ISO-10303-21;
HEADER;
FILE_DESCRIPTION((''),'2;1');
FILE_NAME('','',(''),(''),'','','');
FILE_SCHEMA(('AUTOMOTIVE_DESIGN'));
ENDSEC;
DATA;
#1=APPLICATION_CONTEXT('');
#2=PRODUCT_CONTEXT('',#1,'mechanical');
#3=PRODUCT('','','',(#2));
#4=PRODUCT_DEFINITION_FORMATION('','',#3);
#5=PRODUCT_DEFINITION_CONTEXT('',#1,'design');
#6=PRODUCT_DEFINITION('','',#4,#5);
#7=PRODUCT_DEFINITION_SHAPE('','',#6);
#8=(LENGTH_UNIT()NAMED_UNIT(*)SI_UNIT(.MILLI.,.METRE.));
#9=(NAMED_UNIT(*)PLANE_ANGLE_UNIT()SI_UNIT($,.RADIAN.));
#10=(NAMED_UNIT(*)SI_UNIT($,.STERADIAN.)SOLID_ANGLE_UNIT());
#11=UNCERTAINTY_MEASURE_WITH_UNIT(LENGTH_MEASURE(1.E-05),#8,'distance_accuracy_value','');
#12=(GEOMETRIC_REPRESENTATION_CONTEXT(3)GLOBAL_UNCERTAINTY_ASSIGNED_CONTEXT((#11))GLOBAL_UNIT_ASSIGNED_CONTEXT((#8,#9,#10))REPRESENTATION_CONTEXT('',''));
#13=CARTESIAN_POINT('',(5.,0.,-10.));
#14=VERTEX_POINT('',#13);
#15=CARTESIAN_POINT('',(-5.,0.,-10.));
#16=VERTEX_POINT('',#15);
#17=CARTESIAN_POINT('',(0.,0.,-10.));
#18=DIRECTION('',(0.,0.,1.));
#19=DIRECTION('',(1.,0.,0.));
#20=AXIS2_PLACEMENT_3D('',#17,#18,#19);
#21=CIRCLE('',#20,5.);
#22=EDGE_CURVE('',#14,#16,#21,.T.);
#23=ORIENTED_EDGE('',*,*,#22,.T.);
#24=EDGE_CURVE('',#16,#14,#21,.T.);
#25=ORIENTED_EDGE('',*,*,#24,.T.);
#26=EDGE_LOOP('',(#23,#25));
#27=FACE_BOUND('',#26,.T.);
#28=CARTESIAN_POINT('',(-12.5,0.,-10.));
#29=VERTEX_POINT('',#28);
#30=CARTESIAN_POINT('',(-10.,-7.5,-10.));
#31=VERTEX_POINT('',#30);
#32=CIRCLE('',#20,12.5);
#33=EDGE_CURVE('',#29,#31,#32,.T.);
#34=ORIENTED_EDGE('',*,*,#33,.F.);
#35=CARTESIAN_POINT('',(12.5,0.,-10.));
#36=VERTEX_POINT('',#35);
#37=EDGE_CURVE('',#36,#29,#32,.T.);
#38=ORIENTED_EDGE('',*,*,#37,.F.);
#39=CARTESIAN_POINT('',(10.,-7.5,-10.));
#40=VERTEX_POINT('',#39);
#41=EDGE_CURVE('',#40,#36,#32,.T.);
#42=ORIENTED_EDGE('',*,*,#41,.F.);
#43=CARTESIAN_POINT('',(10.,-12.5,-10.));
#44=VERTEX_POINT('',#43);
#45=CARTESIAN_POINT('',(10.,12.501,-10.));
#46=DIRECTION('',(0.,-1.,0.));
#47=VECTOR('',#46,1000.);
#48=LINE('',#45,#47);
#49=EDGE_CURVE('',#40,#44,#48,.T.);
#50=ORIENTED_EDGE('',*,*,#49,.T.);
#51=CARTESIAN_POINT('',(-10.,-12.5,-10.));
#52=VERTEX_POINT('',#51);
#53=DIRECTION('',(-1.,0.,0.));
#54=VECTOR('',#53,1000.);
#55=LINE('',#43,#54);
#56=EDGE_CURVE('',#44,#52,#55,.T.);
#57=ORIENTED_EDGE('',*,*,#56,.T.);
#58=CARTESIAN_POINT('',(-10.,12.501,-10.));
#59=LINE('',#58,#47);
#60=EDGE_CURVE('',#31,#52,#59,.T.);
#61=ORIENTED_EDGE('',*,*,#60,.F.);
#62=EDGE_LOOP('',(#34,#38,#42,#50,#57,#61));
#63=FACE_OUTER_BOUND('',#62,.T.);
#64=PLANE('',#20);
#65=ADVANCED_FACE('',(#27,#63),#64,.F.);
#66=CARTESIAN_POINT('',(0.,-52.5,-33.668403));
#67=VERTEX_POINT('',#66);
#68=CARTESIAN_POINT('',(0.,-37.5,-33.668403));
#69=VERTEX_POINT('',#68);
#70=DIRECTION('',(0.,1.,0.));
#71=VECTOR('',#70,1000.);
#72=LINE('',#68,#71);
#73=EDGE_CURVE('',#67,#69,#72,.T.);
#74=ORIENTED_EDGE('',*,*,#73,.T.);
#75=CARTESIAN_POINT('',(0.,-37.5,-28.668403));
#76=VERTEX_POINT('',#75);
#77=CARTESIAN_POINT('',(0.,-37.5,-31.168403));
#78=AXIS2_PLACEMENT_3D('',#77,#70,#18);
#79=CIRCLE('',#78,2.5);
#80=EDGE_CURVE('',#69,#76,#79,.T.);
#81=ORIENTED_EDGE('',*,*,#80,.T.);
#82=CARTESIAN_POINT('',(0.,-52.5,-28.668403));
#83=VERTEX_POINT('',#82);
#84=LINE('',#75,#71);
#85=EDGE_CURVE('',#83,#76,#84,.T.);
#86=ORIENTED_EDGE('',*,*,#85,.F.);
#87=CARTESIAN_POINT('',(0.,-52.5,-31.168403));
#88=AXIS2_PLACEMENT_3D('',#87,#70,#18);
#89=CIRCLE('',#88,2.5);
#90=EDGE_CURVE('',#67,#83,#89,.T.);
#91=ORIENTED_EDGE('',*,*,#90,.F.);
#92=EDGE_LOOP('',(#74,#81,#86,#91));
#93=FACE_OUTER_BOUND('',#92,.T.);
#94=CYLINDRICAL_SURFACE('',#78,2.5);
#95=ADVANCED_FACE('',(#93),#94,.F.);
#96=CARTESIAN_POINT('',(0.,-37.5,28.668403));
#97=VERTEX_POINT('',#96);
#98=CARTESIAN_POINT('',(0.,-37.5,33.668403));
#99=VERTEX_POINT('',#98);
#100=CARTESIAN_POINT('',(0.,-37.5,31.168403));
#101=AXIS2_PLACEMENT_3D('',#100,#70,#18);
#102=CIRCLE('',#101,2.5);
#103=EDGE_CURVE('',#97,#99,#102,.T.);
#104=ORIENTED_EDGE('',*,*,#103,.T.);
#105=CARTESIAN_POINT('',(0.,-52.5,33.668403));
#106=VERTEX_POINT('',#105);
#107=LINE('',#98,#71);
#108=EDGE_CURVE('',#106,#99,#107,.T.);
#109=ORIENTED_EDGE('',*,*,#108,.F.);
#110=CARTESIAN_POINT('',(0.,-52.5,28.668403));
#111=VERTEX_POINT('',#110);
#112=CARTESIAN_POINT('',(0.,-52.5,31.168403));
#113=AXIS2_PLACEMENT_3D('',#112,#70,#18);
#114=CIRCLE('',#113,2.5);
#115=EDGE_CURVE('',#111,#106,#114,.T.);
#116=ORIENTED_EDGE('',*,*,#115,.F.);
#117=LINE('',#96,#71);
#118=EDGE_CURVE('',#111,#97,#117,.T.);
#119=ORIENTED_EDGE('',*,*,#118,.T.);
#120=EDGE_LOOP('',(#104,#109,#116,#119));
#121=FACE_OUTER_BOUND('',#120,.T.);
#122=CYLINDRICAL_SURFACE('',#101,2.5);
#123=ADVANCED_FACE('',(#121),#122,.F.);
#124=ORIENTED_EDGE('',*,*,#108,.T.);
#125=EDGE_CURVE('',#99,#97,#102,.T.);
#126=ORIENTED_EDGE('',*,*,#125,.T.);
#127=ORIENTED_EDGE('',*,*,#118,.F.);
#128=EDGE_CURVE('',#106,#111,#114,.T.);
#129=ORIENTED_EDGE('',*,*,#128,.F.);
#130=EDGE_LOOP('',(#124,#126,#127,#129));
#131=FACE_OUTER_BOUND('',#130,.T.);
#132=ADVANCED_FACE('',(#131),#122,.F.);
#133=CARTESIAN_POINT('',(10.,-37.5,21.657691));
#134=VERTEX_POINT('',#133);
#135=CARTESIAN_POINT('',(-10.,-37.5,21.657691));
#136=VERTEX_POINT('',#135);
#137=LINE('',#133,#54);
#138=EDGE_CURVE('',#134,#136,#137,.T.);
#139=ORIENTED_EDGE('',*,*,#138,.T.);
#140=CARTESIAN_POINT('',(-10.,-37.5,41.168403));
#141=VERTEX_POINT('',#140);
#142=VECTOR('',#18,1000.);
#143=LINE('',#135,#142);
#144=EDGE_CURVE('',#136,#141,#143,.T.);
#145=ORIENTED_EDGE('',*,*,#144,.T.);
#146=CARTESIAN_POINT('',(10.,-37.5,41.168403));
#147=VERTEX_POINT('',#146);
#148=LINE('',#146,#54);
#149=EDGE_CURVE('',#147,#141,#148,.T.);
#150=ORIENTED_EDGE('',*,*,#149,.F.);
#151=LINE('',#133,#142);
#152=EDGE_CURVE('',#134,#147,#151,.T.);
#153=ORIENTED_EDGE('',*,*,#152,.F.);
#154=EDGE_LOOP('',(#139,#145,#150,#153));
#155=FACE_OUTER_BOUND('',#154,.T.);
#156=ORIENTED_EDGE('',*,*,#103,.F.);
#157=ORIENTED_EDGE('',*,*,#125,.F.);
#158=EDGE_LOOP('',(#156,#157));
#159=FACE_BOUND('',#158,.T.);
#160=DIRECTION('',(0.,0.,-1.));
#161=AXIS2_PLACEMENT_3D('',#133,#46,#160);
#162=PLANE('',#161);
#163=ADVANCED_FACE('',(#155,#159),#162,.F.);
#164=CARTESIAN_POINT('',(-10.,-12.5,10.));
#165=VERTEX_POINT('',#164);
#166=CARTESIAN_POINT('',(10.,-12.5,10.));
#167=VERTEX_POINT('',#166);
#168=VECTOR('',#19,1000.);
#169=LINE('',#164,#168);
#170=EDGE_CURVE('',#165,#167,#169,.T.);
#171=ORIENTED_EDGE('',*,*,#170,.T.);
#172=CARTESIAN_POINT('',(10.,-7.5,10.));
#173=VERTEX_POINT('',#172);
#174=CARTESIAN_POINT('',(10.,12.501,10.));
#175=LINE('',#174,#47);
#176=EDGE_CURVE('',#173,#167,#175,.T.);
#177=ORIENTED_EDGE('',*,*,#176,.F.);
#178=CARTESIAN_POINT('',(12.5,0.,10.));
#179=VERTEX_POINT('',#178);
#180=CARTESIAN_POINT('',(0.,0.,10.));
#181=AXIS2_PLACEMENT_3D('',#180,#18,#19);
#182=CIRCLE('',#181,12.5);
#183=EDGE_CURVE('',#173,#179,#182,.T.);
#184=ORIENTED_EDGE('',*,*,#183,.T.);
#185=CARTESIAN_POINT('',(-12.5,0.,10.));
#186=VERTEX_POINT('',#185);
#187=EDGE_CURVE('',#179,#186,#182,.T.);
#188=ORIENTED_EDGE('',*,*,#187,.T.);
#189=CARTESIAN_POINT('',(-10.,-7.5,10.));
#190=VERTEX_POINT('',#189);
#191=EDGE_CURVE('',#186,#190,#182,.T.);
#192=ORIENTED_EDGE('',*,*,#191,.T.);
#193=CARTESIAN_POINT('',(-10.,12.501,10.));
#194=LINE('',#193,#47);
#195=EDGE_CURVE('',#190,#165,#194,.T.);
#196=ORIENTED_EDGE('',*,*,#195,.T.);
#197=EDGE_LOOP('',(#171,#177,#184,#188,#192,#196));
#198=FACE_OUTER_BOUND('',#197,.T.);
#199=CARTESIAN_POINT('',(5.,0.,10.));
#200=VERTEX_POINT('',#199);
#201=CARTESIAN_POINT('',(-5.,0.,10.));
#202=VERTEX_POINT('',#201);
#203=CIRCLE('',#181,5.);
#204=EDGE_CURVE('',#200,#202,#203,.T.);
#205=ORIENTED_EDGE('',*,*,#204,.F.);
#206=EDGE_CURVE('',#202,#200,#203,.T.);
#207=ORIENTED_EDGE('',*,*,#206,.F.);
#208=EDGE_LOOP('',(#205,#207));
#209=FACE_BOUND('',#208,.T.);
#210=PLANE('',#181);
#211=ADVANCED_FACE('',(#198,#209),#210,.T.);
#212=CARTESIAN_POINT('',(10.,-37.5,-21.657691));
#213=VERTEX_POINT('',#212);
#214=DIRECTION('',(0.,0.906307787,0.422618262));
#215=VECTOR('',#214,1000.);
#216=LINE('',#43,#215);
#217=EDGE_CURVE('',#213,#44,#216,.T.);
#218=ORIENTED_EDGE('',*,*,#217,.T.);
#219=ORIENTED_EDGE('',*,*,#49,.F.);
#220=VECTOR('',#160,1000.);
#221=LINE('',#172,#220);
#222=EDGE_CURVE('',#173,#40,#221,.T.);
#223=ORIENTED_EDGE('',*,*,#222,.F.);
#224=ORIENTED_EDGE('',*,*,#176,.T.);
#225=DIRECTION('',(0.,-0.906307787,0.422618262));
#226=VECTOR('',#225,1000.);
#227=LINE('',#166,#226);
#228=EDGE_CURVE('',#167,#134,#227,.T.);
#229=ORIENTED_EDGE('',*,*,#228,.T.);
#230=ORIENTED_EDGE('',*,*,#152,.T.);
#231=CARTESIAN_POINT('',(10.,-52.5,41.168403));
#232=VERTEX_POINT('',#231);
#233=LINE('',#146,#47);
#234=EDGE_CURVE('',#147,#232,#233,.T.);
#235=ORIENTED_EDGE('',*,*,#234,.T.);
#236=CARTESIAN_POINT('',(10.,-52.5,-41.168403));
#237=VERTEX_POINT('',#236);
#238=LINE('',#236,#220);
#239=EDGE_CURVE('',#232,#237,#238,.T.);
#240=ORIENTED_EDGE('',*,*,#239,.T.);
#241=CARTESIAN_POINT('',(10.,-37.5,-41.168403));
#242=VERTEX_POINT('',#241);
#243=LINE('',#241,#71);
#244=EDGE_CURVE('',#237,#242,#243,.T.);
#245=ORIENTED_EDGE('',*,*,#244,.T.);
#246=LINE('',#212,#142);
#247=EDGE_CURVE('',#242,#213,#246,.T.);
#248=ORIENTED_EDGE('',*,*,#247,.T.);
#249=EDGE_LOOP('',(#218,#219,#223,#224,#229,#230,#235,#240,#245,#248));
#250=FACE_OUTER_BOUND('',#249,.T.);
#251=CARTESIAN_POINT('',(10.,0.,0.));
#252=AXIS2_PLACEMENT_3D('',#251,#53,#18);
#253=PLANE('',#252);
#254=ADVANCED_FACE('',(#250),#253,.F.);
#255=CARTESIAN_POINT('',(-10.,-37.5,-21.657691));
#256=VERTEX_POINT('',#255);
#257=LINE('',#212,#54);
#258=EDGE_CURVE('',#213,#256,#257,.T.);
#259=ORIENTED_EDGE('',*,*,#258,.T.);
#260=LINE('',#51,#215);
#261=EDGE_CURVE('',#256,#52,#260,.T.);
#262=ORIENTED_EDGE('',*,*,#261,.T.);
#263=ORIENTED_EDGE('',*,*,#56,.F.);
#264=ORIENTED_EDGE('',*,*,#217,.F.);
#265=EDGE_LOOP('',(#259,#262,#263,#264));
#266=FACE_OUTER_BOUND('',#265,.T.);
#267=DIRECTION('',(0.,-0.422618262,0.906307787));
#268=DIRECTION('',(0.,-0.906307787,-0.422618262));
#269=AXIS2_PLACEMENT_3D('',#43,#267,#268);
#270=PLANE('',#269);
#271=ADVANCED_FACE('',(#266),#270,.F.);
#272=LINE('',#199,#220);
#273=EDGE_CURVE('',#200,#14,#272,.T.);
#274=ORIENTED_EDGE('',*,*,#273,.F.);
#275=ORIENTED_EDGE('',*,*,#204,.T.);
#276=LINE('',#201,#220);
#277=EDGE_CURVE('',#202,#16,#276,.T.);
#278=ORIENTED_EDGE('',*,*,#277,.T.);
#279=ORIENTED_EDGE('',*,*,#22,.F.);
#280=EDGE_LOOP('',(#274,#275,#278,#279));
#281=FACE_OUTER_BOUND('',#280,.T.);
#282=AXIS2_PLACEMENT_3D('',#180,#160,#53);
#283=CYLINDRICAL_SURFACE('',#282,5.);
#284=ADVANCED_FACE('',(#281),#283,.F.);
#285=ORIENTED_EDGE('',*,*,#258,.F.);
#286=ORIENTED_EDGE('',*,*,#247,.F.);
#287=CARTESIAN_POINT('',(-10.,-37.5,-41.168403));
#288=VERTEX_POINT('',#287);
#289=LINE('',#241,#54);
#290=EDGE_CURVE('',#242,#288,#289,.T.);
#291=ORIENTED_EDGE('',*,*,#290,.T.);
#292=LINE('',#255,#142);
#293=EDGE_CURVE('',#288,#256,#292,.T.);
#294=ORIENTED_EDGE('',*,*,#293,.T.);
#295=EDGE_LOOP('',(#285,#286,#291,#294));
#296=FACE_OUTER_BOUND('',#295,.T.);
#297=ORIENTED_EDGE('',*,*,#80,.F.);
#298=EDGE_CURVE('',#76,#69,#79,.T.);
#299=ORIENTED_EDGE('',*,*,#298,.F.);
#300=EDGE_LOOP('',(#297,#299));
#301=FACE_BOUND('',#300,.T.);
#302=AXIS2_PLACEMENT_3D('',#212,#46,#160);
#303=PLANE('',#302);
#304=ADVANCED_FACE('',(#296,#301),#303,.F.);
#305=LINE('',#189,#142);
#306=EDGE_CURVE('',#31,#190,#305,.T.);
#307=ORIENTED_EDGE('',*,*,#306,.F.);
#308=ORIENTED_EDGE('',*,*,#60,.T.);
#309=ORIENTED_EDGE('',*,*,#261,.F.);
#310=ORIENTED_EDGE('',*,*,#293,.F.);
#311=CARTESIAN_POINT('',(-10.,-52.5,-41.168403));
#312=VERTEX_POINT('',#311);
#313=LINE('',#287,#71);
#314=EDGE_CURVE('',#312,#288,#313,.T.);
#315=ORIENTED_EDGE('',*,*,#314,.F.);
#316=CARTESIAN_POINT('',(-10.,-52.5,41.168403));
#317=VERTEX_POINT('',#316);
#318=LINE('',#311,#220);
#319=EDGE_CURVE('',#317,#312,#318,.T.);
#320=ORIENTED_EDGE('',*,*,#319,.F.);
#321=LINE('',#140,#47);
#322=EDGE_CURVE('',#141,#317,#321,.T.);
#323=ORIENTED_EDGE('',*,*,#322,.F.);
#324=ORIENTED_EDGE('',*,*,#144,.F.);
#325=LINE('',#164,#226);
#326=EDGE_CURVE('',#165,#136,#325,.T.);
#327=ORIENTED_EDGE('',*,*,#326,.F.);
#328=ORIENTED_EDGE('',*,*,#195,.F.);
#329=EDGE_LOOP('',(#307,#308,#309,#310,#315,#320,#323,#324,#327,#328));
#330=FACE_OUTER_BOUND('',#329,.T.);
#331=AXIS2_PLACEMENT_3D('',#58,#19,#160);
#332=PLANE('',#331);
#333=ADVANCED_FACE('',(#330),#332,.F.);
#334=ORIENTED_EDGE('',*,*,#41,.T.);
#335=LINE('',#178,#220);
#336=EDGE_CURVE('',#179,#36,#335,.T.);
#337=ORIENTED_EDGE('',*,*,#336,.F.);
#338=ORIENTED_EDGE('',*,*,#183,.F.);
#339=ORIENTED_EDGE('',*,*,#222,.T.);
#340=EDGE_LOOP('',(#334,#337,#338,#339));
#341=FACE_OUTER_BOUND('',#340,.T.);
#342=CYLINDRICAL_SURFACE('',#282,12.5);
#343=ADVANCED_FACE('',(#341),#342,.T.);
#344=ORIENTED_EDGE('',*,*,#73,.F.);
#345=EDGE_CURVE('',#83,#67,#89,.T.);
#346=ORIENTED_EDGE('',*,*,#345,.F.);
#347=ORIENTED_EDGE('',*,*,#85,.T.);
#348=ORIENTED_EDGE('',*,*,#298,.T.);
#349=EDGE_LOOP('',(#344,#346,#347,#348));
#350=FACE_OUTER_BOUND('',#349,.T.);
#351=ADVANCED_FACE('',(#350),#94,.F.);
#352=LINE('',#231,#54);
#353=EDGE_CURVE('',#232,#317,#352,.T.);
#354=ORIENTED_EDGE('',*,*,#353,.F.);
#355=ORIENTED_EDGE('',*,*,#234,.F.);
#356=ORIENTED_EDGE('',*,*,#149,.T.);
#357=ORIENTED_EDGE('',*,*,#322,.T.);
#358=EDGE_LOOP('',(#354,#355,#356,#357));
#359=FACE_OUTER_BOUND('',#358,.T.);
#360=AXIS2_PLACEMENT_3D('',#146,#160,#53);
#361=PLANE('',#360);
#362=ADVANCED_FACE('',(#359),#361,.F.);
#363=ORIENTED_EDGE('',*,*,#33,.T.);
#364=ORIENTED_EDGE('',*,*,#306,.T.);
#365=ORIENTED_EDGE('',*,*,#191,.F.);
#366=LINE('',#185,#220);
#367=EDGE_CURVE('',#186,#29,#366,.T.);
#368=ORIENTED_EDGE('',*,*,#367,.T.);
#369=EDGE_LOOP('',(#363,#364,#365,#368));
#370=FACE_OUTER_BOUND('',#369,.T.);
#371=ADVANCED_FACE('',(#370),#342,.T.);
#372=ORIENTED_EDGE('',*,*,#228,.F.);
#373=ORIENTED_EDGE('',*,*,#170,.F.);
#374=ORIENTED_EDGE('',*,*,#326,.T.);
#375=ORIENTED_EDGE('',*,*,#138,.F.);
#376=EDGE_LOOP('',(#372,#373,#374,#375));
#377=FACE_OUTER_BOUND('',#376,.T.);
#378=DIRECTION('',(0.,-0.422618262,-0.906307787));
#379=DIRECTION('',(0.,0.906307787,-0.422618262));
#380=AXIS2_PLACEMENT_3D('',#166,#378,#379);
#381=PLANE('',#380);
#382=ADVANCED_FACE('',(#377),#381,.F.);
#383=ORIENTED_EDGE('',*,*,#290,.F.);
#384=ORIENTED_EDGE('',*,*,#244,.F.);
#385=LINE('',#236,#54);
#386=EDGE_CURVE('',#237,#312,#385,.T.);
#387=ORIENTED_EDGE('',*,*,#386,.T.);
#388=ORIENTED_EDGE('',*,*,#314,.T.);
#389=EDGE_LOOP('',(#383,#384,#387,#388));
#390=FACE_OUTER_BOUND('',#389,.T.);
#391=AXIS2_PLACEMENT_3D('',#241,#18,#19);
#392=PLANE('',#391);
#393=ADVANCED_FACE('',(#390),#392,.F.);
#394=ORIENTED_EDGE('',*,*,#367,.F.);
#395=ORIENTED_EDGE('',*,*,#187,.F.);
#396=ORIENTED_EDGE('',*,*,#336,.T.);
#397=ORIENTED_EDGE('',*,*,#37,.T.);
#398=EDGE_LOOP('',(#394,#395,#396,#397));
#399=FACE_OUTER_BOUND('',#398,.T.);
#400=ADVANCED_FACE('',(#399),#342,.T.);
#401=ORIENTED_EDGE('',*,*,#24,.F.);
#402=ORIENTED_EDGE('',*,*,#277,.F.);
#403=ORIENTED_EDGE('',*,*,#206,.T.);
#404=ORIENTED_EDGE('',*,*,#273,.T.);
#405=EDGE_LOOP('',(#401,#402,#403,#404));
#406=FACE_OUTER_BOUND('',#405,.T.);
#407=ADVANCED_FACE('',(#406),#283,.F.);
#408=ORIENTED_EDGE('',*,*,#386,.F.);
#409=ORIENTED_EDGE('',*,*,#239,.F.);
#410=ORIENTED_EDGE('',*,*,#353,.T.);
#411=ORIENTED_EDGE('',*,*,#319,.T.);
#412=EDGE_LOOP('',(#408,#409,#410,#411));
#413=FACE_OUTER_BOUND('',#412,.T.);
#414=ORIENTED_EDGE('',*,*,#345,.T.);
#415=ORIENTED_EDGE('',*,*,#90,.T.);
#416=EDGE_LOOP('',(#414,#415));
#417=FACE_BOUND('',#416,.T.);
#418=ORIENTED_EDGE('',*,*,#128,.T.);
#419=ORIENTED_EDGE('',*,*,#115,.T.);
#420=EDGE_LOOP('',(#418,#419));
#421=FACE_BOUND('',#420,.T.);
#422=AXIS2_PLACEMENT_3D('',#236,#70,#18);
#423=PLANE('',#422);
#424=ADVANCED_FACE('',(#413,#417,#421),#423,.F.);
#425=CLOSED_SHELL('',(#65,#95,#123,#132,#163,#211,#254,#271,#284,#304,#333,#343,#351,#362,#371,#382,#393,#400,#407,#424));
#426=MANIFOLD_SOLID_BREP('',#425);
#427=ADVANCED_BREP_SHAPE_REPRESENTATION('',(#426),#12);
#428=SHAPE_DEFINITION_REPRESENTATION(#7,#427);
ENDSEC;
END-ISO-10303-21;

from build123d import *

# Parameters (mm, degrees)
SKETCH_1_R           = 12.5
SKETCH_1_R_2         = 5
EXTRUDE_1_DEPTH      = 10
EXTRUDE_3_DEPTH      = 10
EXTRUDE_4_REACH      = 60.746
EXTRUDE_4_END_RADIUS = 12.5
SKETCH_6_W           = 20
SKETCH_6_H           = 20
HOLE_WIZARD_M6_1_D   = 5


with BuildPart() as part:
    # 草图1 → 凸台-拉伸1 (new, symmetric)
    with BuildSketch(Plane.XY):
        Circle(SKETCH_1_R)
        Circle(SKETCH_1_R_2, mode=Mode.SUBTRACT)
    extrude(amount=EXTRUDE_1_DEPTH, both=True)



with BuildPart() as body_2:
    # 草图5 → 凸台-拉伸3 (new, symmetric)
    with BuildSketch(Plane(origin=(0, 0, 0), x_dir=(0, 0, -1), z_dir=(1, 0, 0))):
        Polygon((10, -12.5), (21.657691454, -37.5), (41.168402769, -37.5), (41.168402769, -52.5), (-41.168402769, -52.5), (-41.168402769, -37.5), (-21.657691454, -37.5), (-10, -12.5), align=None)
    extrude(amount=EXTRUDE_3_DEPTH, both=True)


with BuildPart() as part_1:
    add(part.part)

    add(body_2.part)  # 凸台-拉伸4 merges body 2
    # 凸台-拉伸4: up to this cylinder (the profile starts outside it)
    extrude_4_end = Plane(origin=(0, 0, 0), z_dir=(0, 0, -1)) * Cylinder(EXTRUDE_4_END_RADIUS, 147.492, mode=Mode.PRIVATE)
    # 草图6 → 凸台-拉伸4 (add, up to the surface)
    with BuildSketch(Plane(origin=(0, -12.5, 0), x_dir=(1, 0, 0), z_dir=(0, 1, 0)), mode=Mode.PRIVATE) as extrude_4_sk1:
        Rectangle(SKETCH_6_W, SKETCH_6_H)
    extrude_4_tool1 = extrude(extrude_4_sk1.sketch, amount=EXTRUDE_4_REACH, mode=Mode.PRIVATE) - extrude_4_end
    add(extrude_4_tool1.solids().sort_by_distance((0, -12.5, 0))[0])
    add(extrude_4_tool1.solids().sort_by_distance((0, -12.5, 0))[1])

    # M6 螺纹孔1 (through all)
    with Locations(Plane(origin=(0, -37.5, -31.168402769), x_dir=(0, 0, 1), z_dir=(0, 1, 0))):
        with Locations((0, 0)):
            hole_wizard_m6_1 = Hole(HOLE_WIZARD_M6_1_D / 2)

    # 镜向1: M6 螺纹孔1 across plane
    add(hole_wizard_m6_1.mirror(Plane.XY), mode=Mode.SUBTRACT)


solid = part_1.part
